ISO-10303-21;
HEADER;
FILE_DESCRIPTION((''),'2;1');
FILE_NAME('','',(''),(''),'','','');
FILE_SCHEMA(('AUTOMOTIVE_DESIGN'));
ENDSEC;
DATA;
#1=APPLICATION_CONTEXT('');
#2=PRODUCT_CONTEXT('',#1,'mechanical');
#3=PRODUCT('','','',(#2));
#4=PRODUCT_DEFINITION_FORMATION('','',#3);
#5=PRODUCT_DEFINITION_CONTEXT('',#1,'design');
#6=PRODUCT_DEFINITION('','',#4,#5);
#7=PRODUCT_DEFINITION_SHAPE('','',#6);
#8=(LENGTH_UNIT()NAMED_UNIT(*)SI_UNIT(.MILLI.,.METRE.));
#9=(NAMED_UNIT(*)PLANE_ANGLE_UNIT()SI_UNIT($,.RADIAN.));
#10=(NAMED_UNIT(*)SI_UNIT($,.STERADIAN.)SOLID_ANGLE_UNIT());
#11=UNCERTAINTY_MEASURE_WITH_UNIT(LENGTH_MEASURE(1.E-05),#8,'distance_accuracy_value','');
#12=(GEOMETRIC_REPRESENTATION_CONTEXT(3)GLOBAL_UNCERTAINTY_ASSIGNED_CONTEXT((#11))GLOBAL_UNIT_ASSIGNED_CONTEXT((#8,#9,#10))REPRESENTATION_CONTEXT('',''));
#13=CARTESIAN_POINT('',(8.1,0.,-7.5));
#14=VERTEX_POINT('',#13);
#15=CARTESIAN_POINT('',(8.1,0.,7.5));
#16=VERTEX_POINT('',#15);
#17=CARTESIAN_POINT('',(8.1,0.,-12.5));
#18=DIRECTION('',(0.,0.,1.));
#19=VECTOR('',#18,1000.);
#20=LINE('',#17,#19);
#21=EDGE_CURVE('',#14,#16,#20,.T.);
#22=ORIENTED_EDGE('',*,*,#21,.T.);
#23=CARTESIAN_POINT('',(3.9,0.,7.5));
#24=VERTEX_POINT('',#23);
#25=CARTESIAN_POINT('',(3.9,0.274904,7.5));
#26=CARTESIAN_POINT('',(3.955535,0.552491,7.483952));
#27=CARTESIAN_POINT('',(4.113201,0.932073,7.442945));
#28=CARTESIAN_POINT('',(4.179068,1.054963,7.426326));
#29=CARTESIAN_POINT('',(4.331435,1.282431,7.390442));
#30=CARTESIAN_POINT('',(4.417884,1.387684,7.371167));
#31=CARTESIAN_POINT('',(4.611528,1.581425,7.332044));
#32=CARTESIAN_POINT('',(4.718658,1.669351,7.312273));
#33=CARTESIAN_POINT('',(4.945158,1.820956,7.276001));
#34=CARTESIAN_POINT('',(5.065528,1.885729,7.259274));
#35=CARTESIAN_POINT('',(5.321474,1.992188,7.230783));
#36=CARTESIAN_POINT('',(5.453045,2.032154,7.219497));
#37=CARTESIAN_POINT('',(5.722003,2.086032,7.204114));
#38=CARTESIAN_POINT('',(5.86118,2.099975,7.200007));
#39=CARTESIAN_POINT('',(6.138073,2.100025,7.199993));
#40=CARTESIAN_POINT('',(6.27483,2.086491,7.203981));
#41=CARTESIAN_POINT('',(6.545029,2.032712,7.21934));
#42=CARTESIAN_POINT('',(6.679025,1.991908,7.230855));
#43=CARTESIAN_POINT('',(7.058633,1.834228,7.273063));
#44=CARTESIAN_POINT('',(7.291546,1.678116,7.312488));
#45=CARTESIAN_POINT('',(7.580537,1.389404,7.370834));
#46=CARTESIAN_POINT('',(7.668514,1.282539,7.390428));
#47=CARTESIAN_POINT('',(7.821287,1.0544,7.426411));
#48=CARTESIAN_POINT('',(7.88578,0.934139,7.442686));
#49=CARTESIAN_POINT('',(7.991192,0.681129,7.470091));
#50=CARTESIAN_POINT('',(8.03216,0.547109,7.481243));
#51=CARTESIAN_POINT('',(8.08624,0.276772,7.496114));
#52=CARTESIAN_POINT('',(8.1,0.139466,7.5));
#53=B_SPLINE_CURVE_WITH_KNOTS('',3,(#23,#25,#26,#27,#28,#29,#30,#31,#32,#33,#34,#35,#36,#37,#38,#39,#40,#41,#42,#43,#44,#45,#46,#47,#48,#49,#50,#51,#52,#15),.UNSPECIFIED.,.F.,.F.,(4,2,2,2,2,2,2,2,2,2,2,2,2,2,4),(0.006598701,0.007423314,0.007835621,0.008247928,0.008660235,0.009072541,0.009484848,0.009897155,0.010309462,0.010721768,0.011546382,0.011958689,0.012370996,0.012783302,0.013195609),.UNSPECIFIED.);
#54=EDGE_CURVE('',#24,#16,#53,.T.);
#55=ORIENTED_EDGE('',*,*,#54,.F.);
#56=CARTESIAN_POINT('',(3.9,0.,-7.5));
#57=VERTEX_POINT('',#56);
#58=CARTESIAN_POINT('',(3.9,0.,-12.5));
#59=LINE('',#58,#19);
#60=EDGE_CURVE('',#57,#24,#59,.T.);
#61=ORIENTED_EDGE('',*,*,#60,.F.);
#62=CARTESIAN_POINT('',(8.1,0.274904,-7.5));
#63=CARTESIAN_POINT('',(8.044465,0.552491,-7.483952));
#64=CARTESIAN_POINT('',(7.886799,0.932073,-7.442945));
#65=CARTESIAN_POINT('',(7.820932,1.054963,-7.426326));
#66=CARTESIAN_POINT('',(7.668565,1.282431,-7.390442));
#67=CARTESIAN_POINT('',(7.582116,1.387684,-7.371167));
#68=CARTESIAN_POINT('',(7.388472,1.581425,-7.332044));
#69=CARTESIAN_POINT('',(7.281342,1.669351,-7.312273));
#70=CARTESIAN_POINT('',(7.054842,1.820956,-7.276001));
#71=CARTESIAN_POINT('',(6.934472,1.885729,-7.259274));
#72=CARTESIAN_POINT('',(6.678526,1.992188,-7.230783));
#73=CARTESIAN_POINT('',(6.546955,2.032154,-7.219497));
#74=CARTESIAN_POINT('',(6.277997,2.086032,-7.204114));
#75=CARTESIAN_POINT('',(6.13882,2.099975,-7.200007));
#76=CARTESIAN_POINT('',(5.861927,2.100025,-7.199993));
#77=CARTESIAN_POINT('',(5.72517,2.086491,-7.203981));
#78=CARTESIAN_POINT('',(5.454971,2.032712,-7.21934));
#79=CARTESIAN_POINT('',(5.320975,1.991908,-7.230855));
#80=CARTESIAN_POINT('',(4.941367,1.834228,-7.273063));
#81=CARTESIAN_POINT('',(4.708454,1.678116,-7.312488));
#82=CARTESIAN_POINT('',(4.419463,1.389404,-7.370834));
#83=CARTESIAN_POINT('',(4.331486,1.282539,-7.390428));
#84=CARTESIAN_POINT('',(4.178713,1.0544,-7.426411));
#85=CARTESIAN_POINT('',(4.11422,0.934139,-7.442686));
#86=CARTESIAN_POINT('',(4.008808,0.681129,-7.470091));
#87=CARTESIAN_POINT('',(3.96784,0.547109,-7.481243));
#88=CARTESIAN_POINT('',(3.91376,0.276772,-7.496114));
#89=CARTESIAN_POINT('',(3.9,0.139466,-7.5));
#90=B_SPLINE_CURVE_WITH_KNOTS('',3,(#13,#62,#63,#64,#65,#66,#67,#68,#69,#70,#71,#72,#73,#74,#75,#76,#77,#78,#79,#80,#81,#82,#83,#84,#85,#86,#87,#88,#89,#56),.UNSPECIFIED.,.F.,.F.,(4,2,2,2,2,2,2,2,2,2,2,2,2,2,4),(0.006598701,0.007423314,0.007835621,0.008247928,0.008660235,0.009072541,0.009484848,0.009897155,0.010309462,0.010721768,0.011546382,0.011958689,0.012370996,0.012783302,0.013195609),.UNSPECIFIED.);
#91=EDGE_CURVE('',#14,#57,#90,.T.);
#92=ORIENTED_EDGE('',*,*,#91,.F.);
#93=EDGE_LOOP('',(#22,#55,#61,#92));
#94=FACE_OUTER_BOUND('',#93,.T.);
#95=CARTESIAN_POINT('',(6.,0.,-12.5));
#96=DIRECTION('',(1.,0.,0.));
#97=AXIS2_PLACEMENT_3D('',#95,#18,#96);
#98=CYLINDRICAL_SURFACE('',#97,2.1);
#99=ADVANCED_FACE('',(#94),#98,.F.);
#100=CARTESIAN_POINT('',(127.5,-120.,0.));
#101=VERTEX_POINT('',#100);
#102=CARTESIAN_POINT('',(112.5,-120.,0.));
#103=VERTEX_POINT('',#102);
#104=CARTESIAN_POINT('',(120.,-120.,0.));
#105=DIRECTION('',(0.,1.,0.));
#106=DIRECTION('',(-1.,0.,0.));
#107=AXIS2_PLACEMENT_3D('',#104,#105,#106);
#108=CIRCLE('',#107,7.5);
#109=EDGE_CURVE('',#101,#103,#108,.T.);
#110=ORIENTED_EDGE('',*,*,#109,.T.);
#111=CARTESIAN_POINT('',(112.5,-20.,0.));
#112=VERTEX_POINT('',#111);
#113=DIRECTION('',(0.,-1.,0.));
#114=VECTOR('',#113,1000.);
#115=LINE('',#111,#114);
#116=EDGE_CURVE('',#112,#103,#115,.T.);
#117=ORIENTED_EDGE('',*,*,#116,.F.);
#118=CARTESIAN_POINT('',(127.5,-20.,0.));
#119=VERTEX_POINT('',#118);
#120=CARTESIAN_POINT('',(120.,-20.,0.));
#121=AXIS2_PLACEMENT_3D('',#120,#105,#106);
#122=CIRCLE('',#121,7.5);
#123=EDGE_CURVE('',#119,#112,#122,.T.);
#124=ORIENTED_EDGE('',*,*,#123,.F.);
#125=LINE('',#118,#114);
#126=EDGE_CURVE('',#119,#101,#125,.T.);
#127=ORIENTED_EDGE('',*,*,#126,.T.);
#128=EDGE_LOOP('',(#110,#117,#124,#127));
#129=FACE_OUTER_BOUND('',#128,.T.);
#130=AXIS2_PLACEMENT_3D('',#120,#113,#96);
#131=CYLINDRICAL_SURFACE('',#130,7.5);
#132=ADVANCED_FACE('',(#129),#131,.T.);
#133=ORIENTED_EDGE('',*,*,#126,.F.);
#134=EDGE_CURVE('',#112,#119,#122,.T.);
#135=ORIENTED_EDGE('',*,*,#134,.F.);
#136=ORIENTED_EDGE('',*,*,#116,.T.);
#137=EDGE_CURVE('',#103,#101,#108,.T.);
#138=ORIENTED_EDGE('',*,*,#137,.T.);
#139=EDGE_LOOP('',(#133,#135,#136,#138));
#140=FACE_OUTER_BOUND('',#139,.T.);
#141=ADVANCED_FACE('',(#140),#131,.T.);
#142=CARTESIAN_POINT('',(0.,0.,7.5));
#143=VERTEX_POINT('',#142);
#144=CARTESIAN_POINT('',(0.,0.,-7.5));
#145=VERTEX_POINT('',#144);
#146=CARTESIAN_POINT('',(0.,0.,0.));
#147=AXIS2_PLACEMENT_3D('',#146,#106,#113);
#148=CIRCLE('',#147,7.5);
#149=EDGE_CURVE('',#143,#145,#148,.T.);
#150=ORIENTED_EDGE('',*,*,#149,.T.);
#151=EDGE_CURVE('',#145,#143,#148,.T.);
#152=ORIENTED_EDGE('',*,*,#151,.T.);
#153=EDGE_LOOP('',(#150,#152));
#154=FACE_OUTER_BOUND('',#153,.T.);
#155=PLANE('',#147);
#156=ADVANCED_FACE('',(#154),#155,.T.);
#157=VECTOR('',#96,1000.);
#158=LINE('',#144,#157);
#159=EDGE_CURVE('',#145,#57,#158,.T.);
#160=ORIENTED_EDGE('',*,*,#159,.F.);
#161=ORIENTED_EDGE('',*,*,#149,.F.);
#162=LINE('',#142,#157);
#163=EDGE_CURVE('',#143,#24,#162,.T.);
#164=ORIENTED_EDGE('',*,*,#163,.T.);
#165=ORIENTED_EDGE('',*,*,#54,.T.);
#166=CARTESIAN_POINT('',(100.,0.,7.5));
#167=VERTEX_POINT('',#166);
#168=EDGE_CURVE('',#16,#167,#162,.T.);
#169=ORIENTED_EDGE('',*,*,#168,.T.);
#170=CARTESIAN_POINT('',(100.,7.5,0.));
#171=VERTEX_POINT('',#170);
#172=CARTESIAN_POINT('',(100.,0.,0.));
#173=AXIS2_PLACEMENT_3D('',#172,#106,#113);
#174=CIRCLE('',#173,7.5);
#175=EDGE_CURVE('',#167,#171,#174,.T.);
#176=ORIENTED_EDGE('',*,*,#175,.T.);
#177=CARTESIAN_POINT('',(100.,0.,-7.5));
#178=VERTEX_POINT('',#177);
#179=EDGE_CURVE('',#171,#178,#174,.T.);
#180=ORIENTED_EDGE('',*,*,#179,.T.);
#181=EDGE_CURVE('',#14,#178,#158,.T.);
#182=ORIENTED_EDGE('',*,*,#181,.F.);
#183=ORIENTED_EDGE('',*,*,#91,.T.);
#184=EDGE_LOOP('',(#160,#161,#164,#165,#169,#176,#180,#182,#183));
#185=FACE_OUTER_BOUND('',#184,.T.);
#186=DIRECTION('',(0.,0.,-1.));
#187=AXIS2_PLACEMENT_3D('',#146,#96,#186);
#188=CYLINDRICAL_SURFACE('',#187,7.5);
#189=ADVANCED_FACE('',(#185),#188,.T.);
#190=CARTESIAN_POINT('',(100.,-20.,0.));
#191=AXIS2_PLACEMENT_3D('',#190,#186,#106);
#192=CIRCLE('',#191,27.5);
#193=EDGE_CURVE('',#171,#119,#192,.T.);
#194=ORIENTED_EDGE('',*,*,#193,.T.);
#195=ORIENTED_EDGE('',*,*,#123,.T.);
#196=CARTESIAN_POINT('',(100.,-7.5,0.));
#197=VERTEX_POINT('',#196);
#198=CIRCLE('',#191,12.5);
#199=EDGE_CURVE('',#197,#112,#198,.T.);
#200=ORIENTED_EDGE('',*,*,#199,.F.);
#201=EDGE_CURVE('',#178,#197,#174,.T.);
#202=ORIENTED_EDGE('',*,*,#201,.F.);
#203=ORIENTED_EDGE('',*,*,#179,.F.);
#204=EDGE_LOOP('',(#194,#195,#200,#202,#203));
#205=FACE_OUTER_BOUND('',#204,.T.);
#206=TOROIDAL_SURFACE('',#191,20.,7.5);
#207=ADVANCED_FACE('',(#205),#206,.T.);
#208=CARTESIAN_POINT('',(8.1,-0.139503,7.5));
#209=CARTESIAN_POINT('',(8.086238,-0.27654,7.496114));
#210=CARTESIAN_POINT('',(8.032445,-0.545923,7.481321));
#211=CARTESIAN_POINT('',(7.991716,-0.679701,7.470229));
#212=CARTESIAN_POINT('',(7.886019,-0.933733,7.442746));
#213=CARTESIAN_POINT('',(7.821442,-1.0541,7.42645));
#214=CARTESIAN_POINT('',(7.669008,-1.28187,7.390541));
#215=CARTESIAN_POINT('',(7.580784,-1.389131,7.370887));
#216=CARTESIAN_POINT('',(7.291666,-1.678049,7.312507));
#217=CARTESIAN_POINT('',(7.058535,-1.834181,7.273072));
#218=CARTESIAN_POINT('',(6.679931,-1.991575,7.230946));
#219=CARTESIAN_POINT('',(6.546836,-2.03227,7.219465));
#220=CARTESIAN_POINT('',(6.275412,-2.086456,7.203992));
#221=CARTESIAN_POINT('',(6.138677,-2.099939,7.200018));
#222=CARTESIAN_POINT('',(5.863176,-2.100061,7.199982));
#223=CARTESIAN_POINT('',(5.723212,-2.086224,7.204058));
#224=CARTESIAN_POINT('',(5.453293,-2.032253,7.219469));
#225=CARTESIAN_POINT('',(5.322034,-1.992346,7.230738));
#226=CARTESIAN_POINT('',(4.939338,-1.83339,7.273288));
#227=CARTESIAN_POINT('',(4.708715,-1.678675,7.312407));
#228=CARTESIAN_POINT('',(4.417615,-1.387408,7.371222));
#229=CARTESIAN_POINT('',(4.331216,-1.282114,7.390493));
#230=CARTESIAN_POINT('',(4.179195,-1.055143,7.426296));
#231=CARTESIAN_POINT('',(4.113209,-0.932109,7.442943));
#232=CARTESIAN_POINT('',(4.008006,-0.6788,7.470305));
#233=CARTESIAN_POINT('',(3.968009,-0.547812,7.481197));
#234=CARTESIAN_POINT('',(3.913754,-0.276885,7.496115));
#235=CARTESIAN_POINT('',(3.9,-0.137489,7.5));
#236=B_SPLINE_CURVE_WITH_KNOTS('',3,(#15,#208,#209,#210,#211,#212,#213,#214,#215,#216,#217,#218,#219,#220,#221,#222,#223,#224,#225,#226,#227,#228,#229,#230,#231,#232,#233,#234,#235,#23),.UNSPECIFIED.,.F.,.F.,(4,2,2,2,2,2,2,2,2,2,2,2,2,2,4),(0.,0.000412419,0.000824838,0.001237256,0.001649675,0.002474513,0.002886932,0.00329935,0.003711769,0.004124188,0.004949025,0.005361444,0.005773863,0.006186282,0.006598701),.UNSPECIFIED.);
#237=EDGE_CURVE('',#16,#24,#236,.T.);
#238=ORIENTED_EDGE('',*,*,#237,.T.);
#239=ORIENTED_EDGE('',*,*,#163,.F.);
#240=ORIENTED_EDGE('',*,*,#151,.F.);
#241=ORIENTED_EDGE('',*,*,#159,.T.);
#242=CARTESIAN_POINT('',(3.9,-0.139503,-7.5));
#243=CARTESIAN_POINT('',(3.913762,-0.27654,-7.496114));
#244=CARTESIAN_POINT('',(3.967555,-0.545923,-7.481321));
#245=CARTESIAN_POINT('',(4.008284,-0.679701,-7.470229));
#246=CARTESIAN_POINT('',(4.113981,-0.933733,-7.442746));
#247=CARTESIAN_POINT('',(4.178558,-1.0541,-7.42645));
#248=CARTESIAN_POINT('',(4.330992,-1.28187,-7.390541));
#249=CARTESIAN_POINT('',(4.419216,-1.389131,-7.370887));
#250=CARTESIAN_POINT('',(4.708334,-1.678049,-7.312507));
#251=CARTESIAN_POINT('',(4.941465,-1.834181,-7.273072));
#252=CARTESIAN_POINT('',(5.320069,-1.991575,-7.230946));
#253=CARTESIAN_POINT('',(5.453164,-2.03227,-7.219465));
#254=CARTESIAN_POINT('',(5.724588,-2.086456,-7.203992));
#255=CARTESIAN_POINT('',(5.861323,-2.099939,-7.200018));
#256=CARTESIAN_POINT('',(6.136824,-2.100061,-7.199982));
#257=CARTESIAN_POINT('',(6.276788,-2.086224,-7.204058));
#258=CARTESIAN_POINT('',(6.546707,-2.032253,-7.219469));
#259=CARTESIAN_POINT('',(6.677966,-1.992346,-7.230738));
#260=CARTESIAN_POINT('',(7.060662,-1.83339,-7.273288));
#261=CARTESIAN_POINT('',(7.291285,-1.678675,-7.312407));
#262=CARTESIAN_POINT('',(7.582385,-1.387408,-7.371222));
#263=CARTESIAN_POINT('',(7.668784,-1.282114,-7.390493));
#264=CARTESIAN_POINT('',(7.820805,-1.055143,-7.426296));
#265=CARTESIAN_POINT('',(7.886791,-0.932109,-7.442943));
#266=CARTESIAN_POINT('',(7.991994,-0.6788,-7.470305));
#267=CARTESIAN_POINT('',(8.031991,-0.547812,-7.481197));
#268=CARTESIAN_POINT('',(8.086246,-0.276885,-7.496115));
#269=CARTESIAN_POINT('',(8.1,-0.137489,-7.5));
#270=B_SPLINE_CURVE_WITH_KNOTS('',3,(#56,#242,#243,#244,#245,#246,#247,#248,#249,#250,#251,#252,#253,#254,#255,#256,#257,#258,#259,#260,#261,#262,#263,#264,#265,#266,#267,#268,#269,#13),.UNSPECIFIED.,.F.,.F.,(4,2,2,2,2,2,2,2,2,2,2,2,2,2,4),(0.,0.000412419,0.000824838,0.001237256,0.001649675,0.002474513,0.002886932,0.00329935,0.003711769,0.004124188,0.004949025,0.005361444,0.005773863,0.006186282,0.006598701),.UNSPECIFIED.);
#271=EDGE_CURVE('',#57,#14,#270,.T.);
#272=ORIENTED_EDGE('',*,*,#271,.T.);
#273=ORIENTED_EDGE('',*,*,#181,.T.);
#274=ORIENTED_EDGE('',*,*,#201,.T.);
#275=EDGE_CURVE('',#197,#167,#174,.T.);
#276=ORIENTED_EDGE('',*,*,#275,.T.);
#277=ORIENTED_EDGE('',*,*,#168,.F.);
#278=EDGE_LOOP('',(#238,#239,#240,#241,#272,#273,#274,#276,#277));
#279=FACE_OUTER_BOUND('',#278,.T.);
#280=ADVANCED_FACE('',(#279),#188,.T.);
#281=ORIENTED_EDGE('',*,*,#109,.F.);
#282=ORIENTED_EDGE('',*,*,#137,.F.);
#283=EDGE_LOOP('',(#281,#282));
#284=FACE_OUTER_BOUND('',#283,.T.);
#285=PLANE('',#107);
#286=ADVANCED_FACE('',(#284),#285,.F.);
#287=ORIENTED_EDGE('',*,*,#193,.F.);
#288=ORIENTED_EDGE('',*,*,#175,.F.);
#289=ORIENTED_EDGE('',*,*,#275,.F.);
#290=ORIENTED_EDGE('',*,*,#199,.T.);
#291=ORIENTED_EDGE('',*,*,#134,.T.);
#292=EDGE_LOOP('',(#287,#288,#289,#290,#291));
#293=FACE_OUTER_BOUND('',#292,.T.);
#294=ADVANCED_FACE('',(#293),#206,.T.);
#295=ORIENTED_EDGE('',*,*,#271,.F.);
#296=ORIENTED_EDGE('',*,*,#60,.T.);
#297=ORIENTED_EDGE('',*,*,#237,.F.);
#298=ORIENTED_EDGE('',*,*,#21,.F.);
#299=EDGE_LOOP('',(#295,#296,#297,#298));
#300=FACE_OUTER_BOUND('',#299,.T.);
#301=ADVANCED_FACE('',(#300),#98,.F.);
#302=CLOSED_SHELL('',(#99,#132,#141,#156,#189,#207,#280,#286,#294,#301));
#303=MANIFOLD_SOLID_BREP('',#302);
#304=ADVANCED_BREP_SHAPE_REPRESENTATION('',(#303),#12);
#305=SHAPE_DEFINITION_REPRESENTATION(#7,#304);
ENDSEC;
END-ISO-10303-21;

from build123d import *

# Parameters (mm, degrees)
SWEEP_1_PROFILE_R   = 7.5
SKETCH_6_R          = 2.1
CUT_EXTRUDE_1_DEPTH = 20


with BuildPart() as part:
    # 扫描1: sweep along a path in 草图1
    with BuildLine(Plane.XY) as sweep_1_path:
        Line((0, 0), (100, 0))
        ThreePointArc((100, 0), (114.142135624, -5.857864376), (120, -20))
        Line((120, -20), (120, -120))
    # 扫描1 profile (on start of the path) → 扫描1 (sweep)
    with BuildSketch(Plane(origin=(0, 0, 0), x_dir=(0, 0, 1), z_dir=(1, 0, 0))):
        Circle(SWEEP_1_PROFILE_R)
    sweep(path=sweep_1_path.line)

    # 草图6 → 切除-拉伸1 (cut)
    with BuildSketch(Plane.XY.offset(7.5)):
        with Locations((6, 0)):
            Circle(SKETCH_6_R)
    extrude(amount=-CUT_EXTRUDE_1_DEPTH, mode=Mode.SUBTRACT)


solid = part.part
